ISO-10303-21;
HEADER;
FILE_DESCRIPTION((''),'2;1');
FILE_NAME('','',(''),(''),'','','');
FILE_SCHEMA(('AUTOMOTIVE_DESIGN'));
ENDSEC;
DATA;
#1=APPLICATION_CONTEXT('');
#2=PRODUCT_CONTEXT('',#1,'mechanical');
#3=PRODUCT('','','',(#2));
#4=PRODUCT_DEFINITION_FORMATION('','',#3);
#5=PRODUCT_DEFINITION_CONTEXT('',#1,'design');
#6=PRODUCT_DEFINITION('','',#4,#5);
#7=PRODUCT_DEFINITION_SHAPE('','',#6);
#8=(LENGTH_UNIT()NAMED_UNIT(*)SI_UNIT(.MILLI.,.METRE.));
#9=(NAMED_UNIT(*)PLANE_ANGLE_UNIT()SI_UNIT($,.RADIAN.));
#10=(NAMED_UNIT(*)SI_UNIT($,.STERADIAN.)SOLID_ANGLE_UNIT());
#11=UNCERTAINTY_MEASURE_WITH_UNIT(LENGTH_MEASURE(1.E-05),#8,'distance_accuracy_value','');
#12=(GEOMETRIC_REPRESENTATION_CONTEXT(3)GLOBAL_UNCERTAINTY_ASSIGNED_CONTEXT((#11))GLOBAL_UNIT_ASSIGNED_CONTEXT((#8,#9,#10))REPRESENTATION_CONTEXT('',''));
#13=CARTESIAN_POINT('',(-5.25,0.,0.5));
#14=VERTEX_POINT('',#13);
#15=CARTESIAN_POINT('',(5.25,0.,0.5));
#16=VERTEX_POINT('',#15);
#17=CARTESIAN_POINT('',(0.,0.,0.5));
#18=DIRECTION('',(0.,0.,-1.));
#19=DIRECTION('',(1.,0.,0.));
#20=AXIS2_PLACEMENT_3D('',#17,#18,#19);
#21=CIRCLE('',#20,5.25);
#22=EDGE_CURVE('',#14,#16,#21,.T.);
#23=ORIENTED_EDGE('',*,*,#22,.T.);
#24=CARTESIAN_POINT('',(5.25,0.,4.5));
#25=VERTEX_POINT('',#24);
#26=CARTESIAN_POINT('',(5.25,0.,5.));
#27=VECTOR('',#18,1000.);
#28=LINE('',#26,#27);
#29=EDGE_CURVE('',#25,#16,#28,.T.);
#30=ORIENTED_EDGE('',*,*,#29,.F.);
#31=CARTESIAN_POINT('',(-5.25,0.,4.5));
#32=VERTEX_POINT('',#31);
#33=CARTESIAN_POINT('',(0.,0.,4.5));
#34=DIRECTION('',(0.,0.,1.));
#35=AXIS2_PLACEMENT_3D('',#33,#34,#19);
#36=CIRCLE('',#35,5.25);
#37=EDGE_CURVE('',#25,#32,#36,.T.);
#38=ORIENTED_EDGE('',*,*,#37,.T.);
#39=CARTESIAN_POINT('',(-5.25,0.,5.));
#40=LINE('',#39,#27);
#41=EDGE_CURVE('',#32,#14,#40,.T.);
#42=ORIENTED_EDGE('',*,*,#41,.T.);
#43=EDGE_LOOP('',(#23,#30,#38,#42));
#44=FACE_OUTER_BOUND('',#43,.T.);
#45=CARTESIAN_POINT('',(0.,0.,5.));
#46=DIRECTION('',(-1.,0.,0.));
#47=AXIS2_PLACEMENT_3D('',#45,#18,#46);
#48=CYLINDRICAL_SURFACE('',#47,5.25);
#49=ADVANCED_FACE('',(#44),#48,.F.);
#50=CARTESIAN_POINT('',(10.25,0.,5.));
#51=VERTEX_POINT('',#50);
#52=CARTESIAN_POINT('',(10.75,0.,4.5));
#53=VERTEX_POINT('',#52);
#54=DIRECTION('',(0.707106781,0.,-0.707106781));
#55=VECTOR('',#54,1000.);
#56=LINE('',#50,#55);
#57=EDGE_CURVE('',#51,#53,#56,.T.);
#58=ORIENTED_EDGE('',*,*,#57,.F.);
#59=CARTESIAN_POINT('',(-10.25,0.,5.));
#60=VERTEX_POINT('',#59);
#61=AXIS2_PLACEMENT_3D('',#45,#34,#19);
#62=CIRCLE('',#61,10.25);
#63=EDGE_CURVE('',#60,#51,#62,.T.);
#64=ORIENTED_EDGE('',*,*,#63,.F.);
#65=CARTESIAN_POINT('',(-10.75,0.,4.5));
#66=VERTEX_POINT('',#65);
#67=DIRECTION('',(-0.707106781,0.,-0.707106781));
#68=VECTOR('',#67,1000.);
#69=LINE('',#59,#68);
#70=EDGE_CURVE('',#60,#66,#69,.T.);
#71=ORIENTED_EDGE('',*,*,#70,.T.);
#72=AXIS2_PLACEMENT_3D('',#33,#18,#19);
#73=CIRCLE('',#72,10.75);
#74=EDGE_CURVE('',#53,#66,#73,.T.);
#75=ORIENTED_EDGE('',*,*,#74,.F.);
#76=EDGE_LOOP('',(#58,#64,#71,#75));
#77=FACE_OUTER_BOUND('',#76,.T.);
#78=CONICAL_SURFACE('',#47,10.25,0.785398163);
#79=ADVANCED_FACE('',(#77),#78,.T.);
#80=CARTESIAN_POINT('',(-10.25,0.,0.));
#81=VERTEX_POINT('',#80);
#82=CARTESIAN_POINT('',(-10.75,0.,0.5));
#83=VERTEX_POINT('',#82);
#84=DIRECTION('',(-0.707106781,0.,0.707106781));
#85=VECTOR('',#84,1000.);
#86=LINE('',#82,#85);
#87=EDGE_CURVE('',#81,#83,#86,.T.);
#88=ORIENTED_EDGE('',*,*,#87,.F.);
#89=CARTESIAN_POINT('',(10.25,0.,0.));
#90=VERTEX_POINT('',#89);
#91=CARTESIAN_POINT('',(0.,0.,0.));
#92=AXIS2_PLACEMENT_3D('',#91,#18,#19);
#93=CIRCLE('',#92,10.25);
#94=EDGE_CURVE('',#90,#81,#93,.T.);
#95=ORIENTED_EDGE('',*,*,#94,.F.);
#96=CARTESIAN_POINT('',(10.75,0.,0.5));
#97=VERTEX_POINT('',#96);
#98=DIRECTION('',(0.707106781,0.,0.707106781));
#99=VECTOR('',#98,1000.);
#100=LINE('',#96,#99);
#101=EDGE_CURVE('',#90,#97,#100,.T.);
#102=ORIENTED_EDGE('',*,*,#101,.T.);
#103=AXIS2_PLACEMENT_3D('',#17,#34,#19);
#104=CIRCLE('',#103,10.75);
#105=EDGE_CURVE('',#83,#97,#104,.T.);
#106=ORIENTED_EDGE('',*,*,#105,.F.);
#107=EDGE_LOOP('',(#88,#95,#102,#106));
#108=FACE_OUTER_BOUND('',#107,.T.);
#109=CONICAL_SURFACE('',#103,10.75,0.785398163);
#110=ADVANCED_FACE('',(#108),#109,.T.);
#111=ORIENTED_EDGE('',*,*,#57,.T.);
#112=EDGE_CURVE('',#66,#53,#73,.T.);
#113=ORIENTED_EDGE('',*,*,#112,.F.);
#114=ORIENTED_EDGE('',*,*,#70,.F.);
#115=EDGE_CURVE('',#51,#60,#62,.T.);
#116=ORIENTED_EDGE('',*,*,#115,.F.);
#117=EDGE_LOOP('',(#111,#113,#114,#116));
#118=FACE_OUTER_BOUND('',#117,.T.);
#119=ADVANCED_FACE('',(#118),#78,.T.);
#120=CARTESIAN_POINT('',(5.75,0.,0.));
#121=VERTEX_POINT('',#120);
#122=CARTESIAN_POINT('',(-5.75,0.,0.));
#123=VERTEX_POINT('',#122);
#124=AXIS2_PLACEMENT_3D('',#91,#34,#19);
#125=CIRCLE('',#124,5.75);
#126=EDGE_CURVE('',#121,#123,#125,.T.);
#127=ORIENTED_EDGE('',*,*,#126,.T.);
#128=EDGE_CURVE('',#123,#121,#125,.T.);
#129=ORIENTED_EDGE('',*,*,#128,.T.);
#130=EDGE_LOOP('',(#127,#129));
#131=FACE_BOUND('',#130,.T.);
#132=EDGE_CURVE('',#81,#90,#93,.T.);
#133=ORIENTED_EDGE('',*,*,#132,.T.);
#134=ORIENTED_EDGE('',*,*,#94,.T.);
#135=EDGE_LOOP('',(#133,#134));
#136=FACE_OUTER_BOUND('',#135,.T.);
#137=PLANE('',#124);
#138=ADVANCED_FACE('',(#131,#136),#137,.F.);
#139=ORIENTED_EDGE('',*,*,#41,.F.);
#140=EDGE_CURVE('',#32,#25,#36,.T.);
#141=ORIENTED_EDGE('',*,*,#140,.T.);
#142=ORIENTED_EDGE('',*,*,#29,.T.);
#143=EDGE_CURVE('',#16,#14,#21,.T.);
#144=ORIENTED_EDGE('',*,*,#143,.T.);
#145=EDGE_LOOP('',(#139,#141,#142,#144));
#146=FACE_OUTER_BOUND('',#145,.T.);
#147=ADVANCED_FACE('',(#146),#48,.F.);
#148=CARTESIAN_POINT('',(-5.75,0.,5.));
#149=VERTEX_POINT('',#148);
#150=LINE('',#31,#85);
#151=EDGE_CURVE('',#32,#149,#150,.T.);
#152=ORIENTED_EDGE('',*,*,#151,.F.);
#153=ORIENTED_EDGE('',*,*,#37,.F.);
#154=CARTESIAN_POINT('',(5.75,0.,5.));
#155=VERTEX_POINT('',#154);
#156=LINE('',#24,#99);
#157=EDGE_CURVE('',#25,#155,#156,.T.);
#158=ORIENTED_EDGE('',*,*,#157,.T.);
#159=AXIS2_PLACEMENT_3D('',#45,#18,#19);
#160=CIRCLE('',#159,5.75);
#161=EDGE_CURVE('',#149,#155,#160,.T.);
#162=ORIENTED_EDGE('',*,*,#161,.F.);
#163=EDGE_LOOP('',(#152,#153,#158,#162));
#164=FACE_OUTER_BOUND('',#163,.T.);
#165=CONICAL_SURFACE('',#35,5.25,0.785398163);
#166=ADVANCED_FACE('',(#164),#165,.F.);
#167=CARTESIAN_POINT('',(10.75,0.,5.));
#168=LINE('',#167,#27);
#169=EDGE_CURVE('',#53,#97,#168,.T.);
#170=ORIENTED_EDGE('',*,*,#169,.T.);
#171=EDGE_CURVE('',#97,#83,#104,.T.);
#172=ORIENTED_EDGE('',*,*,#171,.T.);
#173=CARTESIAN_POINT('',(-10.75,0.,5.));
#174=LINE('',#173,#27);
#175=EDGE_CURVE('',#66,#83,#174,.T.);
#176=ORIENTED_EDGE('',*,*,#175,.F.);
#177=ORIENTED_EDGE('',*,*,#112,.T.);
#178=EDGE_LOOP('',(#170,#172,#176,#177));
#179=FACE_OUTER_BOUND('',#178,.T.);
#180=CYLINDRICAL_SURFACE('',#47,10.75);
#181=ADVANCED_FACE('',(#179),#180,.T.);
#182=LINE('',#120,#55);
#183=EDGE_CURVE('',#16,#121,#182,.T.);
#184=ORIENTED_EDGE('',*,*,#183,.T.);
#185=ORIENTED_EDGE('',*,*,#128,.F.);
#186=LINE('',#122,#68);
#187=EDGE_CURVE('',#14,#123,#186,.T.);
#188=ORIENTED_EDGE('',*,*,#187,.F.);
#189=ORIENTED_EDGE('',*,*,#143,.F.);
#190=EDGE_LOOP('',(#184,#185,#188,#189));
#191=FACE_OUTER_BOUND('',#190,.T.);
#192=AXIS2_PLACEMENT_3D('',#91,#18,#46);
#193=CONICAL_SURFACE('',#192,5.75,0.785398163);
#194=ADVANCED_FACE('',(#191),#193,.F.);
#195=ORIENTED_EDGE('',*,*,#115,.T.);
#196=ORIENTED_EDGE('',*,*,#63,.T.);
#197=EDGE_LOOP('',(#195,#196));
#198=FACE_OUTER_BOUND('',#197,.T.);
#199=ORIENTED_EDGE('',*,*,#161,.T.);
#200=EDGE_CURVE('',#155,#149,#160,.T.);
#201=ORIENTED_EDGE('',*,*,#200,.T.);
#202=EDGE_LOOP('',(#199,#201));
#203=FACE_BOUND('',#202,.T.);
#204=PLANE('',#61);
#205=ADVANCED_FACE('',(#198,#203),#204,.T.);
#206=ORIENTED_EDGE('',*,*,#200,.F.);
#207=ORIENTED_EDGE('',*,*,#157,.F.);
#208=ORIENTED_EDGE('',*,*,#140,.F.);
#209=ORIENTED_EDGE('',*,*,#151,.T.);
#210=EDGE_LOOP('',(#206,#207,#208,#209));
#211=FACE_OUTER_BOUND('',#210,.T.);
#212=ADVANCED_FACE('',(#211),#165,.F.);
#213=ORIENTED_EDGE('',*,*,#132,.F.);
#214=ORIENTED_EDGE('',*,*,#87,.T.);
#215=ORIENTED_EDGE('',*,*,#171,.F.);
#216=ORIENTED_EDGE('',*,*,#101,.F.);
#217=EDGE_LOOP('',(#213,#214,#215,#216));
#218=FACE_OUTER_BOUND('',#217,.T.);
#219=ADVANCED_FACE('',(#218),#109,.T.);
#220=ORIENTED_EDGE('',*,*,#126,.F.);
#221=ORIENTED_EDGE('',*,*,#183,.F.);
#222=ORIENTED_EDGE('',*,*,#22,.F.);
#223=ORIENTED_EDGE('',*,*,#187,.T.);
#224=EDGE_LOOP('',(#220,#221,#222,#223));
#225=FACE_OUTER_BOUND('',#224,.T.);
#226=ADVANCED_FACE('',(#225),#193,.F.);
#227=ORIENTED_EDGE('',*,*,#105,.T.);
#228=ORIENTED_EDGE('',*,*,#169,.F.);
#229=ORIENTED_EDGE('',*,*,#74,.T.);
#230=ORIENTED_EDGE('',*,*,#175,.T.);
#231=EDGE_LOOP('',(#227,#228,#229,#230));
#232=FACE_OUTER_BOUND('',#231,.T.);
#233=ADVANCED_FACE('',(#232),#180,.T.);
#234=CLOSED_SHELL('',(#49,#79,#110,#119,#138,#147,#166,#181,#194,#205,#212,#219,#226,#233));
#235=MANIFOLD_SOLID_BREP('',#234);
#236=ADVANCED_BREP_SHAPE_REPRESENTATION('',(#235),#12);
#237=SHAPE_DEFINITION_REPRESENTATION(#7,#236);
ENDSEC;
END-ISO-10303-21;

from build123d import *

# Parameters (mm, degrees)
SKETCH1_R           = 10.75
SKETCH1_R_2         = 5.25
BOSS_EXTRUDE1_DEPTH = 5
CHAMFER1_SIZE       = 0.5


with BuildPart() as part:
    # Sketch1 → Boss-Extrude1 (new body)
    with BuildSketch(Plane.XY):
        Circle(SKETCH1_R)
        Circle(SKETCH1_R_2, mode=Mode.SUBTRACT)
    extrude(amount=BOSS_EXTRUDE1_DEPTH)

    # Chamfer1
    chamfer1_edges = [part.edges().sort_by_distance(p)[0] for p in [
        (-10.75, 0, 0),
        (-10.75, 0, 5),
        (-5.25, 0, 0),
        (-5.25, 0, 5),
    ]]
    chamfer(chamfer1_edges, length=CHAMFER1_SIZE)


solid = part.part
